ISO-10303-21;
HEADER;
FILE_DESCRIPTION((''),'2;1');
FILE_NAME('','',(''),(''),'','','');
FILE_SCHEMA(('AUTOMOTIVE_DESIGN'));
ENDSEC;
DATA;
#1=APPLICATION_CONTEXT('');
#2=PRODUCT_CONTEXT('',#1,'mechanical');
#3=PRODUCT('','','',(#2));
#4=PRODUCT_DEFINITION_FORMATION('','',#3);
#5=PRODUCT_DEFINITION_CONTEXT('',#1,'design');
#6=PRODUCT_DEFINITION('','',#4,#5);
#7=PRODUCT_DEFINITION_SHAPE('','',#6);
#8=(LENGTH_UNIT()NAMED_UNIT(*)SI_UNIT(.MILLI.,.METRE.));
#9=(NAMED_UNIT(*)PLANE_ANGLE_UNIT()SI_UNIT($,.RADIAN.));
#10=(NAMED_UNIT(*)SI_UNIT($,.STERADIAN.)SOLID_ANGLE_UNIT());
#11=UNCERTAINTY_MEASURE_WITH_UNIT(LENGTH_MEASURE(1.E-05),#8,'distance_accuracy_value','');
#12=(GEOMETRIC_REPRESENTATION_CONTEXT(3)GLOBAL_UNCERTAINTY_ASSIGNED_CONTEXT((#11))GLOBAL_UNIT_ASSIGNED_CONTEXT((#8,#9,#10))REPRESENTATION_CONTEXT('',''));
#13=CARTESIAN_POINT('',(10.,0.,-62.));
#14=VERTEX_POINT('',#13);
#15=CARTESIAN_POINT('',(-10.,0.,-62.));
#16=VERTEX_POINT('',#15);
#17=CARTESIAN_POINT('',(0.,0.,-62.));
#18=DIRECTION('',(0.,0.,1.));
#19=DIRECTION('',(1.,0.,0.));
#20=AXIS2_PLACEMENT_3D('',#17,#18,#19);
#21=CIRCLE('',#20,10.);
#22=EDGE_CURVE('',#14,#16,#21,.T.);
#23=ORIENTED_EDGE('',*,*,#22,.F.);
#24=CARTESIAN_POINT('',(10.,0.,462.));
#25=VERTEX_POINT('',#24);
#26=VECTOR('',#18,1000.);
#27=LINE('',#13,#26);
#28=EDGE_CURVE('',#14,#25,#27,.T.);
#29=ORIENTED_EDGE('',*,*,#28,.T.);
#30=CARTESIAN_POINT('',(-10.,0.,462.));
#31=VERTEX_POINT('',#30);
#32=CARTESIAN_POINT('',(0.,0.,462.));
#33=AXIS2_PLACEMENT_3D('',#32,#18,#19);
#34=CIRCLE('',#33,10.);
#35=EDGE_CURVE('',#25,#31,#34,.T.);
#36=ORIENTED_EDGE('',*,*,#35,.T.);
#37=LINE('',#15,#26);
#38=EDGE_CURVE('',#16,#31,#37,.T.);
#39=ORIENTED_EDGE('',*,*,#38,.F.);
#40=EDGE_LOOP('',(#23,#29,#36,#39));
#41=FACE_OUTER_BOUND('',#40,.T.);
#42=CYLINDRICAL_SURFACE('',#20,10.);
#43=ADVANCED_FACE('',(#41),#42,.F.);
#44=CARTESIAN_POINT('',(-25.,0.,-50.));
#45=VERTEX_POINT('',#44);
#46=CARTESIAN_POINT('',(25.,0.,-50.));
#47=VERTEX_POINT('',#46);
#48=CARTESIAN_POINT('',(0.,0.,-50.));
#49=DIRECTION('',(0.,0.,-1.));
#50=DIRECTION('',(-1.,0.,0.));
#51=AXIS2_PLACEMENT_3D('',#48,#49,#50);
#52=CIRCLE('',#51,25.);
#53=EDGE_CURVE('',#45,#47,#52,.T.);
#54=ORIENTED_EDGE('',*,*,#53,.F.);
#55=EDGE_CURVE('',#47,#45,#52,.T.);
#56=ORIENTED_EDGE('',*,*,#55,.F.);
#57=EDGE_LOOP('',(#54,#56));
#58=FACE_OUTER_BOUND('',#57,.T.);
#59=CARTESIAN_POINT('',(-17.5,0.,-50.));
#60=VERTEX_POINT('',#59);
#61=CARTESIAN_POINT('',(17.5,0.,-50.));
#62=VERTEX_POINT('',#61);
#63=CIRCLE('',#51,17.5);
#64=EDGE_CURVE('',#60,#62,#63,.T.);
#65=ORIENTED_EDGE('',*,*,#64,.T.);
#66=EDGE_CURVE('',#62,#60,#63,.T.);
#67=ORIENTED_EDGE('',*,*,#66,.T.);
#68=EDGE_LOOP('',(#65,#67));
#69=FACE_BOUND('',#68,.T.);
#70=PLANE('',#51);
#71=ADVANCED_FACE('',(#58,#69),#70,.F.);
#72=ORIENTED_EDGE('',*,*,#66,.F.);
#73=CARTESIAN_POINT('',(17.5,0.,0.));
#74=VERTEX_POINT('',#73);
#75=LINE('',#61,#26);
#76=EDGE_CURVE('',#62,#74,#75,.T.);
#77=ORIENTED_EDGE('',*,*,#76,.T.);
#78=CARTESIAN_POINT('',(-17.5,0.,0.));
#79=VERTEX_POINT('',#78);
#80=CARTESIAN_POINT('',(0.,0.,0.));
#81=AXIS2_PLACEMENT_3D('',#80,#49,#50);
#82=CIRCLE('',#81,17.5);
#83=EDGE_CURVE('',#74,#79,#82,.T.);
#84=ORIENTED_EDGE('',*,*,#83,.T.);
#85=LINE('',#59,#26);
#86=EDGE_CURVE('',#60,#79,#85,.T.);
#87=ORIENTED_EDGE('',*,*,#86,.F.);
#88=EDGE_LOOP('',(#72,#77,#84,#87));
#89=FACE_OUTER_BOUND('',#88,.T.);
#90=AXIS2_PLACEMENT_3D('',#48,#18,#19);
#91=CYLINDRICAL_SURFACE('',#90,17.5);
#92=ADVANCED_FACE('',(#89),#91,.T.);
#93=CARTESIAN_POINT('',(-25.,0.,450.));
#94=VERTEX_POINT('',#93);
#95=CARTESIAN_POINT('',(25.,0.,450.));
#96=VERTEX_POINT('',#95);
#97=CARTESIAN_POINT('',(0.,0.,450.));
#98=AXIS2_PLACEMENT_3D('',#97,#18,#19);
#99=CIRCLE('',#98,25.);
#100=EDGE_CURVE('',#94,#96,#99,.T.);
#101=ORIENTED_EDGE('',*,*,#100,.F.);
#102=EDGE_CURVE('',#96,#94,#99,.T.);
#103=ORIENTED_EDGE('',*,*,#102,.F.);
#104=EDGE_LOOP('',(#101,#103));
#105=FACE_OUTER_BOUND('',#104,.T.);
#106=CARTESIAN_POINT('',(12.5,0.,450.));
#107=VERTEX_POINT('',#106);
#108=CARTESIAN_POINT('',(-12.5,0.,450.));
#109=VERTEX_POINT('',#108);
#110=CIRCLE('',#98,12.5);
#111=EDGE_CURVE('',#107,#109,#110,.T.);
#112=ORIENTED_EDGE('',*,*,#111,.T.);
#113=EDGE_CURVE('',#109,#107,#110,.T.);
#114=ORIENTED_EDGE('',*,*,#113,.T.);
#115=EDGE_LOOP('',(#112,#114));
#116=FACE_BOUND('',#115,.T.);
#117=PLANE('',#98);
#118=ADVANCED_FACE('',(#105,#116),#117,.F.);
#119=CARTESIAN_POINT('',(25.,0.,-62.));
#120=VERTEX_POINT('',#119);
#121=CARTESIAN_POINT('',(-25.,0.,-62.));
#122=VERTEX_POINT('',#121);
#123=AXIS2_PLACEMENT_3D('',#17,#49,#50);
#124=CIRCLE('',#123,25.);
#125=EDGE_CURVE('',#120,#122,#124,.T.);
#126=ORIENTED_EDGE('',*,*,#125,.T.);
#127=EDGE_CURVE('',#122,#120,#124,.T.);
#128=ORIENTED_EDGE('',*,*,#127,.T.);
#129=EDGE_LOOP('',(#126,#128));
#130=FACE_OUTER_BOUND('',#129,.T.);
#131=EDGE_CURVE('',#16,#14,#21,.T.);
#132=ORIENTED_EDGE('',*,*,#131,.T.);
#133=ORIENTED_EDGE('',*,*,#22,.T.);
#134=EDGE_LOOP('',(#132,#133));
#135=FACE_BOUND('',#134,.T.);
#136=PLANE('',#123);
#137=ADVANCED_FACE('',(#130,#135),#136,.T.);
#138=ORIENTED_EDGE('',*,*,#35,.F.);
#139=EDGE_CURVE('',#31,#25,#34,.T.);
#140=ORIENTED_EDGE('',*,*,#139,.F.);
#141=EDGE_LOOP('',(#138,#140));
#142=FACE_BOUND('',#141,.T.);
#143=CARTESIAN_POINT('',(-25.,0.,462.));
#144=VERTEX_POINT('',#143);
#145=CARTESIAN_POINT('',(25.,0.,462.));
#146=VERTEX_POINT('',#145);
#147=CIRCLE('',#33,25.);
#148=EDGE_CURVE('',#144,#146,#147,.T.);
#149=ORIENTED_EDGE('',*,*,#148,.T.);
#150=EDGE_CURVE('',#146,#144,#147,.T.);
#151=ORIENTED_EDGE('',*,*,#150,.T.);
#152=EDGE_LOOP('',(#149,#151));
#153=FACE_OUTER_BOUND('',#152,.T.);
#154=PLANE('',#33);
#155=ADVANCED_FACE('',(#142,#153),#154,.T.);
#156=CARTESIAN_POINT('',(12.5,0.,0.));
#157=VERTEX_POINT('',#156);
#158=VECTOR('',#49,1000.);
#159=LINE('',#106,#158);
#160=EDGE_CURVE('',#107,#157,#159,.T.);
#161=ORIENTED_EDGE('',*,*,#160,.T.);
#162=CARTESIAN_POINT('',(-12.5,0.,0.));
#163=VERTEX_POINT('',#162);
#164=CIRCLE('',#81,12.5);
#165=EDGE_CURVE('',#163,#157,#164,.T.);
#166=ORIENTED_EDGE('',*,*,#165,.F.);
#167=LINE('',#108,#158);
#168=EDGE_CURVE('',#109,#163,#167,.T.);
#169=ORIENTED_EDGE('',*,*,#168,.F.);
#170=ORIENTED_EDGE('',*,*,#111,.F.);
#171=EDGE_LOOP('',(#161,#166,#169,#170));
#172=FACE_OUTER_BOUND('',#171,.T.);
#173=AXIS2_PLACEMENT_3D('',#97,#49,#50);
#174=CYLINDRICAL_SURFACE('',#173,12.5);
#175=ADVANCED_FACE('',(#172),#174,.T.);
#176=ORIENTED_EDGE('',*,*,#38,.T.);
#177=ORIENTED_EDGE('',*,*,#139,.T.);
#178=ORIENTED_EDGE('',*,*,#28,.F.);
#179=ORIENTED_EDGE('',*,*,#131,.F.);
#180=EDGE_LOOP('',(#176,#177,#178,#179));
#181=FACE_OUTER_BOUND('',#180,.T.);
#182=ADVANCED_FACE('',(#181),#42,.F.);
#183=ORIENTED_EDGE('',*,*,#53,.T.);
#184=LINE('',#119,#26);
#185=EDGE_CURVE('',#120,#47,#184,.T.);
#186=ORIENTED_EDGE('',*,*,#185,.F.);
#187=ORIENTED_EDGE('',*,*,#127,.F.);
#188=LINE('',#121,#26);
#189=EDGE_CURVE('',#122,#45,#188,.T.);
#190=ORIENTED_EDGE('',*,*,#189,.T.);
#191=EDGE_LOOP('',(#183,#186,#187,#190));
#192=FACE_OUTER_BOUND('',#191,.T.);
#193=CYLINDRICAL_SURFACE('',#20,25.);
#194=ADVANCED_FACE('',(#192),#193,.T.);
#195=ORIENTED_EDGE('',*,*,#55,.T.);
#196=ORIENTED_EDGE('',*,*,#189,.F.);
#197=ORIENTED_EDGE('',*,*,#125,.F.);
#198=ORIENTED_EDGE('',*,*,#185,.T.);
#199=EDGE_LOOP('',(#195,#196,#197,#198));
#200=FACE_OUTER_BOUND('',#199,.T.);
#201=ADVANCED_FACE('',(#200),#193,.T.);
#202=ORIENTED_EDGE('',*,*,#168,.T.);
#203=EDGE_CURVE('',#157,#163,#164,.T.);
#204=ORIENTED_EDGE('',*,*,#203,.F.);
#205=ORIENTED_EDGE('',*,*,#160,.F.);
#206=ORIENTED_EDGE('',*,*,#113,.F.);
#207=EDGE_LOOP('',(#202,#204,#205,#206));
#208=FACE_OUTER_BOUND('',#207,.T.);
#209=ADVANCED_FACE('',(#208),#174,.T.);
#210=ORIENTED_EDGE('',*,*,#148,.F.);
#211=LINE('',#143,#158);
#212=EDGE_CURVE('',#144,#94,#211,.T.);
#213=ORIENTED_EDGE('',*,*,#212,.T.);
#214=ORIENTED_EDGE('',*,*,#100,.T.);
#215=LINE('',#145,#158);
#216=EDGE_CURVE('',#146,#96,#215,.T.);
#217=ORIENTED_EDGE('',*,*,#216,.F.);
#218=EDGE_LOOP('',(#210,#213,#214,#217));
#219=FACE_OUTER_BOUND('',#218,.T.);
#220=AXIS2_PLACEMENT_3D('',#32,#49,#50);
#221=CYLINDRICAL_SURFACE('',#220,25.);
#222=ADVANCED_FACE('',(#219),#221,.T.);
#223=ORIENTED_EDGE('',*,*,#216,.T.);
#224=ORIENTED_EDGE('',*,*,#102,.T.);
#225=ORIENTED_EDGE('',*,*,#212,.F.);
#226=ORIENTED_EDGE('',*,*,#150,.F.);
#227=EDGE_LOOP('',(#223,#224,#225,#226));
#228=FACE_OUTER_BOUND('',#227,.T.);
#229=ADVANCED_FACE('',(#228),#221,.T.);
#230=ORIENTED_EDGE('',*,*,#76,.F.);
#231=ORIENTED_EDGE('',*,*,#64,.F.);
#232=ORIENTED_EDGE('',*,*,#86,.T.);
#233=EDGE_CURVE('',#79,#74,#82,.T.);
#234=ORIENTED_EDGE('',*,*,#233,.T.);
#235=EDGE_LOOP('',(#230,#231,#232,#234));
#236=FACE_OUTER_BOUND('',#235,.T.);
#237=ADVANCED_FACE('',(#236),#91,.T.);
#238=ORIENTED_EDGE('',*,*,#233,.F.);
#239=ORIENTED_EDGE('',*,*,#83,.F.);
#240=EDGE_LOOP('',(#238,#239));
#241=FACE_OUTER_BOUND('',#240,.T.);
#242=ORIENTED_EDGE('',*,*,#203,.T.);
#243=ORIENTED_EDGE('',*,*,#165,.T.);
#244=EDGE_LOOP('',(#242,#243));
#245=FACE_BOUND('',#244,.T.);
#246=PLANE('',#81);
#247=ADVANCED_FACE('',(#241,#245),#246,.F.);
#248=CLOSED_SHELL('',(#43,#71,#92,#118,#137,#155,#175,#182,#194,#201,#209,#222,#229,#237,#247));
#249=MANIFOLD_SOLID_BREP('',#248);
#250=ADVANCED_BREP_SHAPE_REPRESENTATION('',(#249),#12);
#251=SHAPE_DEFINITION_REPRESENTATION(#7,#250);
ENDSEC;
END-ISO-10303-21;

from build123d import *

# Parameters (mm, degrees)
SKETCH1_R           = 12.5
BOSS_EXTRUDE1_DEPTH = 450
SKETCH2_R           = 17.5
BOSS_EXTRUDE2_DEPTH = 50
SKETCH3_R           = 25
BOSS_EXTRUDE3_DEPTH = 12
BOSS_EXTRUDE4_START = 12
SKETCH4_R           = 25
BOSS_EXTRUDE4_DEPTH = 12
SKETCH5_R           = 10
CUT_EXTRUDE1_DEPTH  = 526.191393684


with BuildPart() as part:
    # Sketch1 → Boss-Extrude1 (new body)
    with BuildSketch(Plane.XY):
        Circle(SKETCH1_R)
    extrude(amount=BOSS_EXTRUDE1_DEPTH)

    # Sketch2 → Boss-Extrude2 (add)
    with BuildSketch(Plane(origin=(0, 0, 0), x_dir=(-1, 0, 0), z_dir=(0, 0, -1))):
        Circle(SKETCH2_R)
    extrude(amount=BOSS_EXTRUDE2_DEPTH)

    # Sketch3 → Boss-Extrude3 (add)
    with BuildSketch(Plane(origin=(0, 0, -50), x_dir=(-1, 0, 0), z_dir=(0, 0, -1))):
        Circle(SKETCH3_R)
    extrude(amount=BOSS_EXTRUDE3_DEPTH)

    # Sketch4 → Boss-Extrude4 (add)
    with BuildSketch(Plane.XY.offset(450).offset(BOSS_EXTRUDE4_START)):
        with Locations(Location((0, 0, 0), (0, 0, 180))):
            Circle(SKETCH4_R)
    extrude(amount=-BOSS_EXTRUDE4_DEPTH)

    # Sketch5 → Cut-Extrude1 (cut, through all)
    with BuildSketch(Plane.XY.offset(462)):
        Circle(SKETCH5_R)
    extrude(amount=-CUT_EXTRUDE1_DEPTH, mode=Mode.SUBTRACT)


solid = part.part
